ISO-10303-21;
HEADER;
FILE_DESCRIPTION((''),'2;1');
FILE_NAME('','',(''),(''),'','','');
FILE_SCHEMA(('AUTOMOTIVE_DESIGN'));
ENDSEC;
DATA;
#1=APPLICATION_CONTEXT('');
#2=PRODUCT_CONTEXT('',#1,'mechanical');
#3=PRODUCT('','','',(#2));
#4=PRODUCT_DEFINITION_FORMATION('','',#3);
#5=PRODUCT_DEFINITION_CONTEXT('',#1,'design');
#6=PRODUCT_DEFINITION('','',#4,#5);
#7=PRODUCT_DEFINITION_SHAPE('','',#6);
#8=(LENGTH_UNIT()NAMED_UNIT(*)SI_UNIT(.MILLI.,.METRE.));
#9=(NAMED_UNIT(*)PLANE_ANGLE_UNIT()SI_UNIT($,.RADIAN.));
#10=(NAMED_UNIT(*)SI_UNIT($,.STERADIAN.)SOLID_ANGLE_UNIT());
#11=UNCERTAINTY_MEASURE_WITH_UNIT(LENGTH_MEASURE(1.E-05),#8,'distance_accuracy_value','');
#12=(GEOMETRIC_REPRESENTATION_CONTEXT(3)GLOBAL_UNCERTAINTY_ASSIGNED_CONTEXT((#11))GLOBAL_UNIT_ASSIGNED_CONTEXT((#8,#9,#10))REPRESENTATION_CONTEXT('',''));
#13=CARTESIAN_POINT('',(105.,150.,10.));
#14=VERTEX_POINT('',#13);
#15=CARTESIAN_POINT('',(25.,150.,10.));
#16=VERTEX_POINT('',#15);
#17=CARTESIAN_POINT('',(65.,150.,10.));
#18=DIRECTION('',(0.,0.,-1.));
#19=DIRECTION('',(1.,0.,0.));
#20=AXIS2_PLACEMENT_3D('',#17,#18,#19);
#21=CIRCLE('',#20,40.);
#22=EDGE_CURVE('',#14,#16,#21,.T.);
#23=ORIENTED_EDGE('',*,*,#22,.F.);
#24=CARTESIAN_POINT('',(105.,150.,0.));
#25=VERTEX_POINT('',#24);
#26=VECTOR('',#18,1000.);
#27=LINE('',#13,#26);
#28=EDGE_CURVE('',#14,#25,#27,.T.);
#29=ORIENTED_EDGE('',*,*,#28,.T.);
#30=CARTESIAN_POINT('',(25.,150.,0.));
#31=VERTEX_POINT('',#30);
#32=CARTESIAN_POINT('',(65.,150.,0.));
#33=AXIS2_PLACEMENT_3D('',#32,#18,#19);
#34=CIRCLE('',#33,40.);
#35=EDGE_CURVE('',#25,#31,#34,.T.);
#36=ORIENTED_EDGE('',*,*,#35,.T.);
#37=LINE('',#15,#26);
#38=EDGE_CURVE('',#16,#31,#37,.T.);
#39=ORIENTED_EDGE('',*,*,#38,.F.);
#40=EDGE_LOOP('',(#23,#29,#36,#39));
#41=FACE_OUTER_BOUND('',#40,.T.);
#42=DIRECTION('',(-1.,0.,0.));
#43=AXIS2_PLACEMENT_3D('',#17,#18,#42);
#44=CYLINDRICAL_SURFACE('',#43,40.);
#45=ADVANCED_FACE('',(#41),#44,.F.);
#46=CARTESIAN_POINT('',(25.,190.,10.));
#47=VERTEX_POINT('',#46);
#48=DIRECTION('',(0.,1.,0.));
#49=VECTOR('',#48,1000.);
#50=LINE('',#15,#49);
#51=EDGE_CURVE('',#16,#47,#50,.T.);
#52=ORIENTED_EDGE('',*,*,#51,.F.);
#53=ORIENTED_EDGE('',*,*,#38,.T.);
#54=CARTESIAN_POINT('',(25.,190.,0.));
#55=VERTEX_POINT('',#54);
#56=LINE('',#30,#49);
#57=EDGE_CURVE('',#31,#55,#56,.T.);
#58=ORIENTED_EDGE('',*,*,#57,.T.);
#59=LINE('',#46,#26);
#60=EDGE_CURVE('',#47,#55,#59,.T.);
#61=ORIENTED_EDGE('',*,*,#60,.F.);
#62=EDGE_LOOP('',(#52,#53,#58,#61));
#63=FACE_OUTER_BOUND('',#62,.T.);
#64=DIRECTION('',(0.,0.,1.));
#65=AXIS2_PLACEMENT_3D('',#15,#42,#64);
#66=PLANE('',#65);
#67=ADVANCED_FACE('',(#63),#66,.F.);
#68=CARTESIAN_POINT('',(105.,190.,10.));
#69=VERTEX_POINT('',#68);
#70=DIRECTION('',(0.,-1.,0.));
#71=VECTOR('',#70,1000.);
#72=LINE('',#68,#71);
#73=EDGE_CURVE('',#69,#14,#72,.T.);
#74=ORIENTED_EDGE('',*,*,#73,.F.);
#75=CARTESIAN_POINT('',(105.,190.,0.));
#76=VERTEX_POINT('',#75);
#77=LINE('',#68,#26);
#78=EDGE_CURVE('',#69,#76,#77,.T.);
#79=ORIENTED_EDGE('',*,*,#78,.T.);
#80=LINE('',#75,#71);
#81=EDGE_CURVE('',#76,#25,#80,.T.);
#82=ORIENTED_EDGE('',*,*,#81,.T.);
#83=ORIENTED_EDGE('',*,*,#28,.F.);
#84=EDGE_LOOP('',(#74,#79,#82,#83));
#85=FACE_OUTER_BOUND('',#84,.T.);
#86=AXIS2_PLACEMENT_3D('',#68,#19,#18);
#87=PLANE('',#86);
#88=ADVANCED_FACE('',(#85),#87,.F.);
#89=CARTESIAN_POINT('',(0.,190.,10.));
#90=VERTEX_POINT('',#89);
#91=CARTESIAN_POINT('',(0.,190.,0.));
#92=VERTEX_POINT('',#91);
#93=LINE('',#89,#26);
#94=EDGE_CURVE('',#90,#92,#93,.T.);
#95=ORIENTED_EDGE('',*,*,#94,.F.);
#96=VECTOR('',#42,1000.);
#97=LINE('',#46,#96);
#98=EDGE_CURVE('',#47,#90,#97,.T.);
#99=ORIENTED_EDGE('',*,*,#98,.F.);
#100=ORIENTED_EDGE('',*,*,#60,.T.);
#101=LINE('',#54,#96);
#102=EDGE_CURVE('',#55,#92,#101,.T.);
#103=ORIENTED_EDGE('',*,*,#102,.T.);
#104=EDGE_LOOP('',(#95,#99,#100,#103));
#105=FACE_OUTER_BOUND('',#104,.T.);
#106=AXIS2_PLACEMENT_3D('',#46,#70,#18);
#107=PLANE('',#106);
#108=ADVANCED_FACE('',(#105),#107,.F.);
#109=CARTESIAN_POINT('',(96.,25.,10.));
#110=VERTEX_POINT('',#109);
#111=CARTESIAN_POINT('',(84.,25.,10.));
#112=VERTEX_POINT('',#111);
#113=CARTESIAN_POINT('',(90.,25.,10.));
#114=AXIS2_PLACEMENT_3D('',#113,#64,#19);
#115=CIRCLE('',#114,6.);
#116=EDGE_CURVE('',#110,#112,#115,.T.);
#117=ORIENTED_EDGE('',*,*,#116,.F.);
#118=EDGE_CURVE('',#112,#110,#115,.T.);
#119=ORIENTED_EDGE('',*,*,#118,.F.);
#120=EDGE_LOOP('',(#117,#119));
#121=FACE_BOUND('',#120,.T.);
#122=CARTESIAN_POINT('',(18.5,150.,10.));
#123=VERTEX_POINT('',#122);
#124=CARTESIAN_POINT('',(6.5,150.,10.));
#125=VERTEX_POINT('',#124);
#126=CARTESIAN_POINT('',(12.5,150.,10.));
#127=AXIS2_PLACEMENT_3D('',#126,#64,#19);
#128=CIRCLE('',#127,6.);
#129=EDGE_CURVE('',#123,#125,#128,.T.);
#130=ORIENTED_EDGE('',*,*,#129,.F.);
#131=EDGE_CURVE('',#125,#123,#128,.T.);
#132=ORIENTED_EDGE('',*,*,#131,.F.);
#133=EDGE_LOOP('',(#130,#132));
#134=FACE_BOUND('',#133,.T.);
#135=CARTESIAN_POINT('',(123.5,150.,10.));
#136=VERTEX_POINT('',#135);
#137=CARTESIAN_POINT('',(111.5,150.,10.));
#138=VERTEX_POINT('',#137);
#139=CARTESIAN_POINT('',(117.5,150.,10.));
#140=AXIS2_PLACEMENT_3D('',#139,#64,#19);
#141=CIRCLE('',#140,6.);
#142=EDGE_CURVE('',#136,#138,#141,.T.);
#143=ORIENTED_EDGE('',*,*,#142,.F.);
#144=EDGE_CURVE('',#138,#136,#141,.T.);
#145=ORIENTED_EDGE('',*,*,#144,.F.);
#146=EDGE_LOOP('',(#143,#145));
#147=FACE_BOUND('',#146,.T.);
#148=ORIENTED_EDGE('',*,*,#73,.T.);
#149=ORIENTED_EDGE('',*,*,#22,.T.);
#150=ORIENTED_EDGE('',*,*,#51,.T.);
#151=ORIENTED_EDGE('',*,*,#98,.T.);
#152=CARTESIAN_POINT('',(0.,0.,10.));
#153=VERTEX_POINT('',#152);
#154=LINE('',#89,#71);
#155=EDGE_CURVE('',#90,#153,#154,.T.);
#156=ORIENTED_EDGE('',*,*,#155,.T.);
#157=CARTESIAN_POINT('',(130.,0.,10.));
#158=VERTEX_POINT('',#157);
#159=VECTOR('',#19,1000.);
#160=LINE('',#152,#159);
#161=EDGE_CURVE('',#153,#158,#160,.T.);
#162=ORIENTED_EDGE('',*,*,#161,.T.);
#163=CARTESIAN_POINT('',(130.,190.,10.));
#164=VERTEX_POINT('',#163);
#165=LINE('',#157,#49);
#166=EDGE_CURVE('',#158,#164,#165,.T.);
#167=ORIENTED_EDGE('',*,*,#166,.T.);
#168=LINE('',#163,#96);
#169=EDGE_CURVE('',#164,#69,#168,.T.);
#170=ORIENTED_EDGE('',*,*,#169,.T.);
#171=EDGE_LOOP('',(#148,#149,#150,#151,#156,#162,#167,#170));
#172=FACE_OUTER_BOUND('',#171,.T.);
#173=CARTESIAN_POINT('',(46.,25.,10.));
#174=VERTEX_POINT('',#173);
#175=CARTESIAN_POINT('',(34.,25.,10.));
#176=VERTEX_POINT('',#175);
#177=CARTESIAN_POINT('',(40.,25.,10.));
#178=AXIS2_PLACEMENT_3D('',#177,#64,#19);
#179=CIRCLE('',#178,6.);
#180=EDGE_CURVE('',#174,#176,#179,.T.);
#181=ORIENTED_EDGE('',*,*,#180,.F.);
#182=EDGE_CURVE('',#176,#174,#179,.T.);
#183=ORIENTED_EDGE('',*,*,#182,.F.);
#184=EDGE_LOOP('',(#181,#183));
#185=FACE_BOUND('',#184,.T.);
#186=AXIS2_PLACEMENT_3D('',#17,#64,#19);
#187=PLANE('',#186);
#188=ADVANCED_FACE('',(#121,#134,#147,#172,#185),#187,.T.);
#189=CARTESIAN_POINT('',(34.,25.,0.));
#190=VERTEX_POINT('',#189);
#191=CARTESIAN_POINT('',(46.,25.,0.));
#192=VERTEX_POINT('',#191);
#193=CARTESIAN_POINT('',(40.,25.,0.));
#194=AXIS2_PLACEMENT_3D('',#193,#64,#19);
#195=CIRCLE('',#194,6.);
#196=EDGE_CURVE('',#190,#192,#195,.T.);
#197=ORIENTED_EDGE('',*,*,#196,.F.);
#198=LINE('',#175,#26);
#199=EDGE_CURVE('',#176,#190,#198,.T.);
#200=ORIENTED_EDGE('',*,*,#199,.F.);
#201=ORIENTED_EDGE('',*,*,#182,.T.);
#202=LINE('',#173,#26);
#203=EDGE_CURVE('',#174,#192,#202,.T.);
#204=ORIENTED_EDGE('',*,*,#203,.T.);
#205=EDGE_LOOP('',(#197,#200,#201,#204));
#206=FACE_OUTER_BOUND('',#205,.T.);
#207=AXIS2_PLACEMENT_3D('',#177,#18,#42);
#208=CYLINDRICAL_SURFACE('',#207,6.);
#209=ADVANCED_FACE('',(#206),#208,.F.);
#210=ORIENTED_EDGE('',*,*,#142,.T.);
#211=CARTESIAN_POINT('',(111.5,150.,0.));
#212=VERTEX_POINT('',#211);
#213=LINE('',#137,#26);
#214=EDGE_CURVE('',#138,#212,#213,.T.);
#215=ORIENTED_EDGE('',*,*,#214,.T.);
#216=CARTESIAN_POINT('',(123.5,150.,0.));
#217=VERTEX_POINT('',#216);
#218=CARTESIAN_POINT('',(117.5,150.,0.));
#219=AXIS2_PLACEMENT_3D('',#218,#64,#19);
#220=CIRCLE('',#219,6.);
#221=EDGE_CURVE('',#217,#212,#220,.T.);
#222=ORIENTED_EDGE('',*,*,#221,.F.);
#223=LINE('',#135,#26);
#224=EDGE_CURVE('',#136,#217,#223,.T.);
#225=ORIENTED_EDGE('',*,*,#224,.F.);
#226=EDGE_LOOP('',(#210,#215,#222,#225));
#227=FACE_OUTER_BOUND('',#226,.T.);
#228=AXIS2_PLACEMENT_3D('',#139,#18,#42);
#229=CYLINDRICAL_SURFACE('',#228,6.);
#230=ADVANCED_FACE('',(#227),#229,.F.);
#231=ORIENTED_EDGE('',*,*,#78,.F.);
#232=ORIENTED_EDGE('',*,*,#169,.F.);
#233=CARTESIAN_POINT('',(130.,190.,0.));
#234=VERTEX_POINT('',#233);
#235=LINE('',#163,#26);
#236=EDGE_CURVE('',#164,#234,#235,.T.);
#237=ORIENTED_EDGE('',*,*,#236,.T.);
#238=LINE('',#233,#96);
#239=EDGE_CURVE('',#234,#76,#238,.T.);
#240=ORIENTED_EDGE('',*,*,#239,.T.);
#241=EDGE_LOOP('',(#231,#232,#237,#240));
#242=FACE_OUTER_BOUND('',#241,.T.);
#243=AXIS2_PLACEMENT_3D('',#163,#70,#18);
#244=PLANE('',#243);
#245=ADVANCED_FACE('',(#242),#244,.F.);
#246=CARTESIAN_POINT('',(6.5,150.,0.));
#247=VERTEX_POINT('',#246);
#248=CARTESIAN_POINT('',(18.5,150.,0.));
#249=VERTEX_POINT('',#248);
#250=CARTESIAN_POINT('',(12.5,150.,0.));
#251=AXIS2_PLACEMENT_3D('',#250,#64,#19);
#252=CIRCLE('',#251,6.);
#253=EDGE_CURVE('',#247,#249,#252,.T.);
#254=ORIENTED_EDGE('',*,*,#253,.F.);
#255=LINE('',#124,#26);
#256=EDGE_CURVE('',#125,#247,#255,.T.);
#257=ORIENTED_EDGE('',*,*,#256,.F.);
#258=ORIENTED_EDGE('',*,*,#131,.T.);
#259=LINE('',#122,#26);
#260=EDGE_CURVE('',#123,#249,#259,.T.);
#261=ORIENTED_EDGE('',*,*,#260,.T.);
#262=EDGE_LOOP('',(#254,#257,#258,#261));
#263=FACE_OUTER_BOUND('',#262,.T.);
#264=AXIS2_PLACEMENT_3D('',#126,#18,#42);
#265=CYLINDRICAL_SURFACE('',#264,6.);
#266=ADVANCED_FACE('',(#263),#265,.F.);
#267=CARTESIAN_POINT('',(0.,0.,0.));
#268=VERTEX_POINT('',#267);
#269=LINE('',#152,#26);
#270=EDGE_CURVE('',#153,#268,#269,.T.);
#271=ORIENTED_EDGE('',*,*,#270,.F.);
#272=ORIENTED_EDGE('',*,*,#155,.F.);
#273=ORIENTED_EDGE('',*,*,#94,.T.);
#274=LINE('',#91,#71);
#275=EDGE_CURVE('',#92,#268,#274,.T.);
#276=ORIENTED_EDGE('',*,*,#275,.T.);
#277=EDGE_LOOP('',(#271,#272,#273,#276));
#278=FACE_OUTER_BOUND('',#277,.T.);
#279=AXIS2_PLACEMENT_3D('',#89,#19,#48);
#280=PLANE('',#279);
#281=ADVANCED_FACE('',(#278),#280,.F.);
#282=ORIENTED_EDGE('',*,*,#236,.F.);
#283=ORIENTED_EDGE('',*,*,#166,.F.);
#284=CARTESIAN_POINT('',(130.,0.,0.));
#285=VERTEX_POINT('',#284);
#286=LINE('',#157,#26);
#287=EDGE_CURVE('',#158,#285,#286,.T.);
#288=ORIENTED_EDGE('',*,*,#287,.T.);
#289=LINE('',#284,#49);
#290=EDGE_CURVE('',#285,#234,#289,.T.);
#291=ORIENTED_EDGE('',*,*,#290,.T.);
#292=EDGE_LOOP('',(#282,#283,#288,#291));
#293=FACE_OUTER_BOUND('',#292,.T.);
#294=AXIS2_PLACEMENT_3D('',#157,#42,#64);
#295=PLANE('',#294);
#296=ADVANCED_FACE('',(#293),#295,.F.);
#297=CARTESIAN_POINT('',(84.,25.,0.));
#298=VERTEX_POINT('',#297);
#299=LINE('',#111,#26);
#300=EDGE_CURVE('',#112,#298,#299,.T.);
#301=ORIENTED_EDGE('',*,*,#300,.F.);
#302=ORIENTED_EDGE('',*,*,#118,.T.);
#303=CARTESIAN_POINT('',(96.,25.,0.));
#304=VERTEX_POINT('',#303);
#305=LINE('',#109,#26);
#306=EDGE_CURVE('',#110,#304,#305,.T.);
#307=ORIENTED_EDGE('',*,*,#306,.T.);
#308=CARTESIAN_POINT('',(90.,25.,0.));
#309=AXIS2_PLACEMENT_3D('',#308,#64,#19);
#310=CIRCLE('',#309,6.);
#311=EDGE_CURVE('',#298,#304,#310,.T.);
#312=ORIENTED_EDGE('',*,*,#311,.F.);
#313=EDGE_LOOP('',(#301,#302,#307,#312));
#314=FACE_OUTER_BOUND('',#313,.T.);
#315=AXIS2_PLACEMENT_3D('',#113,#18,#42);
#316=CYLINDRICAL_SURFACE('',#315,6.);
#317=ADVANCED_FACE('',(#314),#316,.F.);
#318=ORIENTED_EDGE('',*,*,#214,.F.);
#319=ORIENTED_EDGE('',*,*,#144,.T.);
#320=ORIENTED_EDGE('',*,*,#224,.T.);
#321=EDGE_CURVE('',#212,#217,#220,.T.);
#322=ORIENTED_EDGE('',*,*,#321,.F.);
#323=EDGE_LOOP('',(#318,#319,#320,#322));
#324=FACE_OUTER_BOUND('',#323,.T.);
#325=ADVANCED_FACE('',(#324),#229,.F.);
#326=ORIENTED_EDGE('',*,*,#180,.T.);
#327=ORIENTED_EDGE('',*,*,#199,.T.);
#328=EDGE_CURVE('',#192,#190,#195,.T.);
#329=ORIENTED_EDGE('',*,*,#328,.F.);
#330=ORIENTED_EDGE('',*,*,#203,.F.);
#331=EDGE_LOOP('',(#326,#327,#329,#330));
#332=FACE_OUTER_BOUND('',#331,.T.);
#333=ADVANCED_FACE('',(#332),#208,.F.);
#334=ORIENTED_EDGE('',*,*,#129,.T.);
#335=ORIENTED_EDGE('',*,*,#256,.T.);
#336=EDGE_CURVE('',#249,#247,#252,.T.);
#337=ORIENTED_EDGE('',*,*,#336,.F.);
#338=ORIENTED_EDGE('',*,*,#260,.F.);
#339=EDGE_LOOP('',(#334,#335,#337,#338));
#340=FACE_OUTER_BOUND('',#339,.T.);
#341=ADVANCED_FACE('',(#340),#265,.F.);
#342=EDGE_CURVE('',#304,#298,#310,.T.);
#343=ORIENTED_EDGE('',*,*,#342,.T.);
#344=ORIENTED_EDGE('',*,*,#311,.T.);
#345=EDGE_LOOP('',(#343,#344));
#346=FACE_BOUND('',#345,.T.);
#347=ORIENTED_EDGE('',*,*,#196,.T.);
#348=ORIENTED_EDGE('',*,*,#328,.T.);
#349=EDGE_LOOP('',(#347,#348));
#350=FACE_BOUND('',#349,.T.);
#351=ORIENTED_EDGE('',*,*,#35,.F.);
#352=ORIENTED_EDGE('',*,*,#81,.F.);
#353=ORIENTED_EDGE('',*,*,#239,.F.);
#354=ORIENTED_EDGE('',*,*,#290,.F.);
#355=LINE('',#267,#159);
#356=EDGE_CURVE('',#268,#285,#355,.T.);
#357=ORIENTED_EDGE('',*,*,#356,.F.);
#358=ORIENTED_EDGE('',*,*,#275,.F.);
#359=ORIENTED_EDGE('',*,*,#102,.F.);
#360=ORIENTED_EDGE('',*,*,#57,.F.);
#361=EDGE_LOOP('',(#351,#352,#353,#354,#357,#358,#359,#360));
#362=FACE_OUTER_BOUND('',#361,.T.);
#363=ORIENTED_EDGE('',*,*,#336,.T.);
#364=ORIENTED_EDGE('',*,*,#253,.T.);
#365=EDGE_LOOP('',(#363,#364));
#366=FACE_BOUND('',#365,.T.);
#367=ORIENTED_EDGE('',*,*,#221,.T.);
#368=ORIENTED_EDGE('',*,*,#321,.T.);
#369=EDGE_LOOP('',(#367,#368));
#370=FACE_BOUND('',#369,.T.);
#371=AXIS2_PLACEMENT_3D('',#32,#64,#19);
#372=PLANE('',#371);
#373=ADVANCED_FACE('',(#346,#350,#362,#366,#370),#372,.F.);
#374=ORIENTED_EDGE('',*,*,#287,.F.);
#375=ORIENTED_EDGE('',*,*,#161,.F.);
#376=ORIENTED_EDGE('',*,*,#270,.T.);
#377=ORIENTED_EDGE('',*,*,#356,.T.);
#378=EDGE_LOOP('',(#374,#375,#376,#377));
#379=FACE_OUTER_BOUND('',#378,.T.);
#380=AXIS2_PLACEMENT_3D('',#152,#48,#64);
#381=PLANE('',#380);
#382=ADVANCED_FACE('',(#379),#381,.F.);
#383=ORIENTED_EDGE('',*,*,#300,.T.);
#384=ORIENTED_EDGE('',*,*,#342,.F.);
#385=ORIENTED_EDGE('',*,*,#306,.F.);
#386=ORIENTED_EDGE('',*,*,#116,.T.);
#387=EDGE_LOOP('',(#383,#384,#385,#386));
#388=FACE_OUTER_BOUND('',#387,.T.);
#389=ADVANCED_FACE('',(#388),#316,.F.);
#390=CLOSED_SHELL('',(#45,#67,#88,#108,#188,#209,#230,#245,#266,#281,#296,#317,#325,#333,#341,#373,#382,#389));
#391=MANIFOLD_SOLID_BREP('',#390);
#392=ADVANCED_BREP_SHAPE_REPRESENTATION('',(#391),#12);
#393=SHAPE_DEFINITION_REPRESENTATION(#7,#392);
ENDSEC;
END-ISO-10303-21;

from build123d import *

# Parameters (mm, degrees)
SKETCH_1_R      = 6
EXTRUDE_1_DEPTH = 10


with BuildPart() as part:
    # 草图1 → 凸台-拉伸1 (new body)
    with BuildSketch(Plane.XY):
        with BuildLine():
            Line((0, 0), (130, 0))
            Line((130, 0), (130, 190))
            Line((130, 190), (105, 190))
            Line((105, 190), (105, 150))
            ThreePointArc((105, 150), (65, 110), (25, 150))
            Line((25, 150), (25, 190))
            Line((25, 190), (0, 190))
            Line((0, 190), (0, 0))
        make_face()
        with Locations((117.5, 150)):
            Circle(SKETCH_1_R, mode=Mode.SUBTRACT)
        with Locations((12.5, 150)):
            Circle(SKETCH_1_R, mode=Mode.SUBTRACT)
        with Locations((40, 25)):
            Circle(SKETCH_1_R, mode=Mode.SUBTRACT)
        with Locations((90, 25)):
            Circle(SKETCH_1_R, mode=Mode.SUBTRACT)
    extrude(amount=EXTRUDE_1_DEPTH)


solid = part.part
